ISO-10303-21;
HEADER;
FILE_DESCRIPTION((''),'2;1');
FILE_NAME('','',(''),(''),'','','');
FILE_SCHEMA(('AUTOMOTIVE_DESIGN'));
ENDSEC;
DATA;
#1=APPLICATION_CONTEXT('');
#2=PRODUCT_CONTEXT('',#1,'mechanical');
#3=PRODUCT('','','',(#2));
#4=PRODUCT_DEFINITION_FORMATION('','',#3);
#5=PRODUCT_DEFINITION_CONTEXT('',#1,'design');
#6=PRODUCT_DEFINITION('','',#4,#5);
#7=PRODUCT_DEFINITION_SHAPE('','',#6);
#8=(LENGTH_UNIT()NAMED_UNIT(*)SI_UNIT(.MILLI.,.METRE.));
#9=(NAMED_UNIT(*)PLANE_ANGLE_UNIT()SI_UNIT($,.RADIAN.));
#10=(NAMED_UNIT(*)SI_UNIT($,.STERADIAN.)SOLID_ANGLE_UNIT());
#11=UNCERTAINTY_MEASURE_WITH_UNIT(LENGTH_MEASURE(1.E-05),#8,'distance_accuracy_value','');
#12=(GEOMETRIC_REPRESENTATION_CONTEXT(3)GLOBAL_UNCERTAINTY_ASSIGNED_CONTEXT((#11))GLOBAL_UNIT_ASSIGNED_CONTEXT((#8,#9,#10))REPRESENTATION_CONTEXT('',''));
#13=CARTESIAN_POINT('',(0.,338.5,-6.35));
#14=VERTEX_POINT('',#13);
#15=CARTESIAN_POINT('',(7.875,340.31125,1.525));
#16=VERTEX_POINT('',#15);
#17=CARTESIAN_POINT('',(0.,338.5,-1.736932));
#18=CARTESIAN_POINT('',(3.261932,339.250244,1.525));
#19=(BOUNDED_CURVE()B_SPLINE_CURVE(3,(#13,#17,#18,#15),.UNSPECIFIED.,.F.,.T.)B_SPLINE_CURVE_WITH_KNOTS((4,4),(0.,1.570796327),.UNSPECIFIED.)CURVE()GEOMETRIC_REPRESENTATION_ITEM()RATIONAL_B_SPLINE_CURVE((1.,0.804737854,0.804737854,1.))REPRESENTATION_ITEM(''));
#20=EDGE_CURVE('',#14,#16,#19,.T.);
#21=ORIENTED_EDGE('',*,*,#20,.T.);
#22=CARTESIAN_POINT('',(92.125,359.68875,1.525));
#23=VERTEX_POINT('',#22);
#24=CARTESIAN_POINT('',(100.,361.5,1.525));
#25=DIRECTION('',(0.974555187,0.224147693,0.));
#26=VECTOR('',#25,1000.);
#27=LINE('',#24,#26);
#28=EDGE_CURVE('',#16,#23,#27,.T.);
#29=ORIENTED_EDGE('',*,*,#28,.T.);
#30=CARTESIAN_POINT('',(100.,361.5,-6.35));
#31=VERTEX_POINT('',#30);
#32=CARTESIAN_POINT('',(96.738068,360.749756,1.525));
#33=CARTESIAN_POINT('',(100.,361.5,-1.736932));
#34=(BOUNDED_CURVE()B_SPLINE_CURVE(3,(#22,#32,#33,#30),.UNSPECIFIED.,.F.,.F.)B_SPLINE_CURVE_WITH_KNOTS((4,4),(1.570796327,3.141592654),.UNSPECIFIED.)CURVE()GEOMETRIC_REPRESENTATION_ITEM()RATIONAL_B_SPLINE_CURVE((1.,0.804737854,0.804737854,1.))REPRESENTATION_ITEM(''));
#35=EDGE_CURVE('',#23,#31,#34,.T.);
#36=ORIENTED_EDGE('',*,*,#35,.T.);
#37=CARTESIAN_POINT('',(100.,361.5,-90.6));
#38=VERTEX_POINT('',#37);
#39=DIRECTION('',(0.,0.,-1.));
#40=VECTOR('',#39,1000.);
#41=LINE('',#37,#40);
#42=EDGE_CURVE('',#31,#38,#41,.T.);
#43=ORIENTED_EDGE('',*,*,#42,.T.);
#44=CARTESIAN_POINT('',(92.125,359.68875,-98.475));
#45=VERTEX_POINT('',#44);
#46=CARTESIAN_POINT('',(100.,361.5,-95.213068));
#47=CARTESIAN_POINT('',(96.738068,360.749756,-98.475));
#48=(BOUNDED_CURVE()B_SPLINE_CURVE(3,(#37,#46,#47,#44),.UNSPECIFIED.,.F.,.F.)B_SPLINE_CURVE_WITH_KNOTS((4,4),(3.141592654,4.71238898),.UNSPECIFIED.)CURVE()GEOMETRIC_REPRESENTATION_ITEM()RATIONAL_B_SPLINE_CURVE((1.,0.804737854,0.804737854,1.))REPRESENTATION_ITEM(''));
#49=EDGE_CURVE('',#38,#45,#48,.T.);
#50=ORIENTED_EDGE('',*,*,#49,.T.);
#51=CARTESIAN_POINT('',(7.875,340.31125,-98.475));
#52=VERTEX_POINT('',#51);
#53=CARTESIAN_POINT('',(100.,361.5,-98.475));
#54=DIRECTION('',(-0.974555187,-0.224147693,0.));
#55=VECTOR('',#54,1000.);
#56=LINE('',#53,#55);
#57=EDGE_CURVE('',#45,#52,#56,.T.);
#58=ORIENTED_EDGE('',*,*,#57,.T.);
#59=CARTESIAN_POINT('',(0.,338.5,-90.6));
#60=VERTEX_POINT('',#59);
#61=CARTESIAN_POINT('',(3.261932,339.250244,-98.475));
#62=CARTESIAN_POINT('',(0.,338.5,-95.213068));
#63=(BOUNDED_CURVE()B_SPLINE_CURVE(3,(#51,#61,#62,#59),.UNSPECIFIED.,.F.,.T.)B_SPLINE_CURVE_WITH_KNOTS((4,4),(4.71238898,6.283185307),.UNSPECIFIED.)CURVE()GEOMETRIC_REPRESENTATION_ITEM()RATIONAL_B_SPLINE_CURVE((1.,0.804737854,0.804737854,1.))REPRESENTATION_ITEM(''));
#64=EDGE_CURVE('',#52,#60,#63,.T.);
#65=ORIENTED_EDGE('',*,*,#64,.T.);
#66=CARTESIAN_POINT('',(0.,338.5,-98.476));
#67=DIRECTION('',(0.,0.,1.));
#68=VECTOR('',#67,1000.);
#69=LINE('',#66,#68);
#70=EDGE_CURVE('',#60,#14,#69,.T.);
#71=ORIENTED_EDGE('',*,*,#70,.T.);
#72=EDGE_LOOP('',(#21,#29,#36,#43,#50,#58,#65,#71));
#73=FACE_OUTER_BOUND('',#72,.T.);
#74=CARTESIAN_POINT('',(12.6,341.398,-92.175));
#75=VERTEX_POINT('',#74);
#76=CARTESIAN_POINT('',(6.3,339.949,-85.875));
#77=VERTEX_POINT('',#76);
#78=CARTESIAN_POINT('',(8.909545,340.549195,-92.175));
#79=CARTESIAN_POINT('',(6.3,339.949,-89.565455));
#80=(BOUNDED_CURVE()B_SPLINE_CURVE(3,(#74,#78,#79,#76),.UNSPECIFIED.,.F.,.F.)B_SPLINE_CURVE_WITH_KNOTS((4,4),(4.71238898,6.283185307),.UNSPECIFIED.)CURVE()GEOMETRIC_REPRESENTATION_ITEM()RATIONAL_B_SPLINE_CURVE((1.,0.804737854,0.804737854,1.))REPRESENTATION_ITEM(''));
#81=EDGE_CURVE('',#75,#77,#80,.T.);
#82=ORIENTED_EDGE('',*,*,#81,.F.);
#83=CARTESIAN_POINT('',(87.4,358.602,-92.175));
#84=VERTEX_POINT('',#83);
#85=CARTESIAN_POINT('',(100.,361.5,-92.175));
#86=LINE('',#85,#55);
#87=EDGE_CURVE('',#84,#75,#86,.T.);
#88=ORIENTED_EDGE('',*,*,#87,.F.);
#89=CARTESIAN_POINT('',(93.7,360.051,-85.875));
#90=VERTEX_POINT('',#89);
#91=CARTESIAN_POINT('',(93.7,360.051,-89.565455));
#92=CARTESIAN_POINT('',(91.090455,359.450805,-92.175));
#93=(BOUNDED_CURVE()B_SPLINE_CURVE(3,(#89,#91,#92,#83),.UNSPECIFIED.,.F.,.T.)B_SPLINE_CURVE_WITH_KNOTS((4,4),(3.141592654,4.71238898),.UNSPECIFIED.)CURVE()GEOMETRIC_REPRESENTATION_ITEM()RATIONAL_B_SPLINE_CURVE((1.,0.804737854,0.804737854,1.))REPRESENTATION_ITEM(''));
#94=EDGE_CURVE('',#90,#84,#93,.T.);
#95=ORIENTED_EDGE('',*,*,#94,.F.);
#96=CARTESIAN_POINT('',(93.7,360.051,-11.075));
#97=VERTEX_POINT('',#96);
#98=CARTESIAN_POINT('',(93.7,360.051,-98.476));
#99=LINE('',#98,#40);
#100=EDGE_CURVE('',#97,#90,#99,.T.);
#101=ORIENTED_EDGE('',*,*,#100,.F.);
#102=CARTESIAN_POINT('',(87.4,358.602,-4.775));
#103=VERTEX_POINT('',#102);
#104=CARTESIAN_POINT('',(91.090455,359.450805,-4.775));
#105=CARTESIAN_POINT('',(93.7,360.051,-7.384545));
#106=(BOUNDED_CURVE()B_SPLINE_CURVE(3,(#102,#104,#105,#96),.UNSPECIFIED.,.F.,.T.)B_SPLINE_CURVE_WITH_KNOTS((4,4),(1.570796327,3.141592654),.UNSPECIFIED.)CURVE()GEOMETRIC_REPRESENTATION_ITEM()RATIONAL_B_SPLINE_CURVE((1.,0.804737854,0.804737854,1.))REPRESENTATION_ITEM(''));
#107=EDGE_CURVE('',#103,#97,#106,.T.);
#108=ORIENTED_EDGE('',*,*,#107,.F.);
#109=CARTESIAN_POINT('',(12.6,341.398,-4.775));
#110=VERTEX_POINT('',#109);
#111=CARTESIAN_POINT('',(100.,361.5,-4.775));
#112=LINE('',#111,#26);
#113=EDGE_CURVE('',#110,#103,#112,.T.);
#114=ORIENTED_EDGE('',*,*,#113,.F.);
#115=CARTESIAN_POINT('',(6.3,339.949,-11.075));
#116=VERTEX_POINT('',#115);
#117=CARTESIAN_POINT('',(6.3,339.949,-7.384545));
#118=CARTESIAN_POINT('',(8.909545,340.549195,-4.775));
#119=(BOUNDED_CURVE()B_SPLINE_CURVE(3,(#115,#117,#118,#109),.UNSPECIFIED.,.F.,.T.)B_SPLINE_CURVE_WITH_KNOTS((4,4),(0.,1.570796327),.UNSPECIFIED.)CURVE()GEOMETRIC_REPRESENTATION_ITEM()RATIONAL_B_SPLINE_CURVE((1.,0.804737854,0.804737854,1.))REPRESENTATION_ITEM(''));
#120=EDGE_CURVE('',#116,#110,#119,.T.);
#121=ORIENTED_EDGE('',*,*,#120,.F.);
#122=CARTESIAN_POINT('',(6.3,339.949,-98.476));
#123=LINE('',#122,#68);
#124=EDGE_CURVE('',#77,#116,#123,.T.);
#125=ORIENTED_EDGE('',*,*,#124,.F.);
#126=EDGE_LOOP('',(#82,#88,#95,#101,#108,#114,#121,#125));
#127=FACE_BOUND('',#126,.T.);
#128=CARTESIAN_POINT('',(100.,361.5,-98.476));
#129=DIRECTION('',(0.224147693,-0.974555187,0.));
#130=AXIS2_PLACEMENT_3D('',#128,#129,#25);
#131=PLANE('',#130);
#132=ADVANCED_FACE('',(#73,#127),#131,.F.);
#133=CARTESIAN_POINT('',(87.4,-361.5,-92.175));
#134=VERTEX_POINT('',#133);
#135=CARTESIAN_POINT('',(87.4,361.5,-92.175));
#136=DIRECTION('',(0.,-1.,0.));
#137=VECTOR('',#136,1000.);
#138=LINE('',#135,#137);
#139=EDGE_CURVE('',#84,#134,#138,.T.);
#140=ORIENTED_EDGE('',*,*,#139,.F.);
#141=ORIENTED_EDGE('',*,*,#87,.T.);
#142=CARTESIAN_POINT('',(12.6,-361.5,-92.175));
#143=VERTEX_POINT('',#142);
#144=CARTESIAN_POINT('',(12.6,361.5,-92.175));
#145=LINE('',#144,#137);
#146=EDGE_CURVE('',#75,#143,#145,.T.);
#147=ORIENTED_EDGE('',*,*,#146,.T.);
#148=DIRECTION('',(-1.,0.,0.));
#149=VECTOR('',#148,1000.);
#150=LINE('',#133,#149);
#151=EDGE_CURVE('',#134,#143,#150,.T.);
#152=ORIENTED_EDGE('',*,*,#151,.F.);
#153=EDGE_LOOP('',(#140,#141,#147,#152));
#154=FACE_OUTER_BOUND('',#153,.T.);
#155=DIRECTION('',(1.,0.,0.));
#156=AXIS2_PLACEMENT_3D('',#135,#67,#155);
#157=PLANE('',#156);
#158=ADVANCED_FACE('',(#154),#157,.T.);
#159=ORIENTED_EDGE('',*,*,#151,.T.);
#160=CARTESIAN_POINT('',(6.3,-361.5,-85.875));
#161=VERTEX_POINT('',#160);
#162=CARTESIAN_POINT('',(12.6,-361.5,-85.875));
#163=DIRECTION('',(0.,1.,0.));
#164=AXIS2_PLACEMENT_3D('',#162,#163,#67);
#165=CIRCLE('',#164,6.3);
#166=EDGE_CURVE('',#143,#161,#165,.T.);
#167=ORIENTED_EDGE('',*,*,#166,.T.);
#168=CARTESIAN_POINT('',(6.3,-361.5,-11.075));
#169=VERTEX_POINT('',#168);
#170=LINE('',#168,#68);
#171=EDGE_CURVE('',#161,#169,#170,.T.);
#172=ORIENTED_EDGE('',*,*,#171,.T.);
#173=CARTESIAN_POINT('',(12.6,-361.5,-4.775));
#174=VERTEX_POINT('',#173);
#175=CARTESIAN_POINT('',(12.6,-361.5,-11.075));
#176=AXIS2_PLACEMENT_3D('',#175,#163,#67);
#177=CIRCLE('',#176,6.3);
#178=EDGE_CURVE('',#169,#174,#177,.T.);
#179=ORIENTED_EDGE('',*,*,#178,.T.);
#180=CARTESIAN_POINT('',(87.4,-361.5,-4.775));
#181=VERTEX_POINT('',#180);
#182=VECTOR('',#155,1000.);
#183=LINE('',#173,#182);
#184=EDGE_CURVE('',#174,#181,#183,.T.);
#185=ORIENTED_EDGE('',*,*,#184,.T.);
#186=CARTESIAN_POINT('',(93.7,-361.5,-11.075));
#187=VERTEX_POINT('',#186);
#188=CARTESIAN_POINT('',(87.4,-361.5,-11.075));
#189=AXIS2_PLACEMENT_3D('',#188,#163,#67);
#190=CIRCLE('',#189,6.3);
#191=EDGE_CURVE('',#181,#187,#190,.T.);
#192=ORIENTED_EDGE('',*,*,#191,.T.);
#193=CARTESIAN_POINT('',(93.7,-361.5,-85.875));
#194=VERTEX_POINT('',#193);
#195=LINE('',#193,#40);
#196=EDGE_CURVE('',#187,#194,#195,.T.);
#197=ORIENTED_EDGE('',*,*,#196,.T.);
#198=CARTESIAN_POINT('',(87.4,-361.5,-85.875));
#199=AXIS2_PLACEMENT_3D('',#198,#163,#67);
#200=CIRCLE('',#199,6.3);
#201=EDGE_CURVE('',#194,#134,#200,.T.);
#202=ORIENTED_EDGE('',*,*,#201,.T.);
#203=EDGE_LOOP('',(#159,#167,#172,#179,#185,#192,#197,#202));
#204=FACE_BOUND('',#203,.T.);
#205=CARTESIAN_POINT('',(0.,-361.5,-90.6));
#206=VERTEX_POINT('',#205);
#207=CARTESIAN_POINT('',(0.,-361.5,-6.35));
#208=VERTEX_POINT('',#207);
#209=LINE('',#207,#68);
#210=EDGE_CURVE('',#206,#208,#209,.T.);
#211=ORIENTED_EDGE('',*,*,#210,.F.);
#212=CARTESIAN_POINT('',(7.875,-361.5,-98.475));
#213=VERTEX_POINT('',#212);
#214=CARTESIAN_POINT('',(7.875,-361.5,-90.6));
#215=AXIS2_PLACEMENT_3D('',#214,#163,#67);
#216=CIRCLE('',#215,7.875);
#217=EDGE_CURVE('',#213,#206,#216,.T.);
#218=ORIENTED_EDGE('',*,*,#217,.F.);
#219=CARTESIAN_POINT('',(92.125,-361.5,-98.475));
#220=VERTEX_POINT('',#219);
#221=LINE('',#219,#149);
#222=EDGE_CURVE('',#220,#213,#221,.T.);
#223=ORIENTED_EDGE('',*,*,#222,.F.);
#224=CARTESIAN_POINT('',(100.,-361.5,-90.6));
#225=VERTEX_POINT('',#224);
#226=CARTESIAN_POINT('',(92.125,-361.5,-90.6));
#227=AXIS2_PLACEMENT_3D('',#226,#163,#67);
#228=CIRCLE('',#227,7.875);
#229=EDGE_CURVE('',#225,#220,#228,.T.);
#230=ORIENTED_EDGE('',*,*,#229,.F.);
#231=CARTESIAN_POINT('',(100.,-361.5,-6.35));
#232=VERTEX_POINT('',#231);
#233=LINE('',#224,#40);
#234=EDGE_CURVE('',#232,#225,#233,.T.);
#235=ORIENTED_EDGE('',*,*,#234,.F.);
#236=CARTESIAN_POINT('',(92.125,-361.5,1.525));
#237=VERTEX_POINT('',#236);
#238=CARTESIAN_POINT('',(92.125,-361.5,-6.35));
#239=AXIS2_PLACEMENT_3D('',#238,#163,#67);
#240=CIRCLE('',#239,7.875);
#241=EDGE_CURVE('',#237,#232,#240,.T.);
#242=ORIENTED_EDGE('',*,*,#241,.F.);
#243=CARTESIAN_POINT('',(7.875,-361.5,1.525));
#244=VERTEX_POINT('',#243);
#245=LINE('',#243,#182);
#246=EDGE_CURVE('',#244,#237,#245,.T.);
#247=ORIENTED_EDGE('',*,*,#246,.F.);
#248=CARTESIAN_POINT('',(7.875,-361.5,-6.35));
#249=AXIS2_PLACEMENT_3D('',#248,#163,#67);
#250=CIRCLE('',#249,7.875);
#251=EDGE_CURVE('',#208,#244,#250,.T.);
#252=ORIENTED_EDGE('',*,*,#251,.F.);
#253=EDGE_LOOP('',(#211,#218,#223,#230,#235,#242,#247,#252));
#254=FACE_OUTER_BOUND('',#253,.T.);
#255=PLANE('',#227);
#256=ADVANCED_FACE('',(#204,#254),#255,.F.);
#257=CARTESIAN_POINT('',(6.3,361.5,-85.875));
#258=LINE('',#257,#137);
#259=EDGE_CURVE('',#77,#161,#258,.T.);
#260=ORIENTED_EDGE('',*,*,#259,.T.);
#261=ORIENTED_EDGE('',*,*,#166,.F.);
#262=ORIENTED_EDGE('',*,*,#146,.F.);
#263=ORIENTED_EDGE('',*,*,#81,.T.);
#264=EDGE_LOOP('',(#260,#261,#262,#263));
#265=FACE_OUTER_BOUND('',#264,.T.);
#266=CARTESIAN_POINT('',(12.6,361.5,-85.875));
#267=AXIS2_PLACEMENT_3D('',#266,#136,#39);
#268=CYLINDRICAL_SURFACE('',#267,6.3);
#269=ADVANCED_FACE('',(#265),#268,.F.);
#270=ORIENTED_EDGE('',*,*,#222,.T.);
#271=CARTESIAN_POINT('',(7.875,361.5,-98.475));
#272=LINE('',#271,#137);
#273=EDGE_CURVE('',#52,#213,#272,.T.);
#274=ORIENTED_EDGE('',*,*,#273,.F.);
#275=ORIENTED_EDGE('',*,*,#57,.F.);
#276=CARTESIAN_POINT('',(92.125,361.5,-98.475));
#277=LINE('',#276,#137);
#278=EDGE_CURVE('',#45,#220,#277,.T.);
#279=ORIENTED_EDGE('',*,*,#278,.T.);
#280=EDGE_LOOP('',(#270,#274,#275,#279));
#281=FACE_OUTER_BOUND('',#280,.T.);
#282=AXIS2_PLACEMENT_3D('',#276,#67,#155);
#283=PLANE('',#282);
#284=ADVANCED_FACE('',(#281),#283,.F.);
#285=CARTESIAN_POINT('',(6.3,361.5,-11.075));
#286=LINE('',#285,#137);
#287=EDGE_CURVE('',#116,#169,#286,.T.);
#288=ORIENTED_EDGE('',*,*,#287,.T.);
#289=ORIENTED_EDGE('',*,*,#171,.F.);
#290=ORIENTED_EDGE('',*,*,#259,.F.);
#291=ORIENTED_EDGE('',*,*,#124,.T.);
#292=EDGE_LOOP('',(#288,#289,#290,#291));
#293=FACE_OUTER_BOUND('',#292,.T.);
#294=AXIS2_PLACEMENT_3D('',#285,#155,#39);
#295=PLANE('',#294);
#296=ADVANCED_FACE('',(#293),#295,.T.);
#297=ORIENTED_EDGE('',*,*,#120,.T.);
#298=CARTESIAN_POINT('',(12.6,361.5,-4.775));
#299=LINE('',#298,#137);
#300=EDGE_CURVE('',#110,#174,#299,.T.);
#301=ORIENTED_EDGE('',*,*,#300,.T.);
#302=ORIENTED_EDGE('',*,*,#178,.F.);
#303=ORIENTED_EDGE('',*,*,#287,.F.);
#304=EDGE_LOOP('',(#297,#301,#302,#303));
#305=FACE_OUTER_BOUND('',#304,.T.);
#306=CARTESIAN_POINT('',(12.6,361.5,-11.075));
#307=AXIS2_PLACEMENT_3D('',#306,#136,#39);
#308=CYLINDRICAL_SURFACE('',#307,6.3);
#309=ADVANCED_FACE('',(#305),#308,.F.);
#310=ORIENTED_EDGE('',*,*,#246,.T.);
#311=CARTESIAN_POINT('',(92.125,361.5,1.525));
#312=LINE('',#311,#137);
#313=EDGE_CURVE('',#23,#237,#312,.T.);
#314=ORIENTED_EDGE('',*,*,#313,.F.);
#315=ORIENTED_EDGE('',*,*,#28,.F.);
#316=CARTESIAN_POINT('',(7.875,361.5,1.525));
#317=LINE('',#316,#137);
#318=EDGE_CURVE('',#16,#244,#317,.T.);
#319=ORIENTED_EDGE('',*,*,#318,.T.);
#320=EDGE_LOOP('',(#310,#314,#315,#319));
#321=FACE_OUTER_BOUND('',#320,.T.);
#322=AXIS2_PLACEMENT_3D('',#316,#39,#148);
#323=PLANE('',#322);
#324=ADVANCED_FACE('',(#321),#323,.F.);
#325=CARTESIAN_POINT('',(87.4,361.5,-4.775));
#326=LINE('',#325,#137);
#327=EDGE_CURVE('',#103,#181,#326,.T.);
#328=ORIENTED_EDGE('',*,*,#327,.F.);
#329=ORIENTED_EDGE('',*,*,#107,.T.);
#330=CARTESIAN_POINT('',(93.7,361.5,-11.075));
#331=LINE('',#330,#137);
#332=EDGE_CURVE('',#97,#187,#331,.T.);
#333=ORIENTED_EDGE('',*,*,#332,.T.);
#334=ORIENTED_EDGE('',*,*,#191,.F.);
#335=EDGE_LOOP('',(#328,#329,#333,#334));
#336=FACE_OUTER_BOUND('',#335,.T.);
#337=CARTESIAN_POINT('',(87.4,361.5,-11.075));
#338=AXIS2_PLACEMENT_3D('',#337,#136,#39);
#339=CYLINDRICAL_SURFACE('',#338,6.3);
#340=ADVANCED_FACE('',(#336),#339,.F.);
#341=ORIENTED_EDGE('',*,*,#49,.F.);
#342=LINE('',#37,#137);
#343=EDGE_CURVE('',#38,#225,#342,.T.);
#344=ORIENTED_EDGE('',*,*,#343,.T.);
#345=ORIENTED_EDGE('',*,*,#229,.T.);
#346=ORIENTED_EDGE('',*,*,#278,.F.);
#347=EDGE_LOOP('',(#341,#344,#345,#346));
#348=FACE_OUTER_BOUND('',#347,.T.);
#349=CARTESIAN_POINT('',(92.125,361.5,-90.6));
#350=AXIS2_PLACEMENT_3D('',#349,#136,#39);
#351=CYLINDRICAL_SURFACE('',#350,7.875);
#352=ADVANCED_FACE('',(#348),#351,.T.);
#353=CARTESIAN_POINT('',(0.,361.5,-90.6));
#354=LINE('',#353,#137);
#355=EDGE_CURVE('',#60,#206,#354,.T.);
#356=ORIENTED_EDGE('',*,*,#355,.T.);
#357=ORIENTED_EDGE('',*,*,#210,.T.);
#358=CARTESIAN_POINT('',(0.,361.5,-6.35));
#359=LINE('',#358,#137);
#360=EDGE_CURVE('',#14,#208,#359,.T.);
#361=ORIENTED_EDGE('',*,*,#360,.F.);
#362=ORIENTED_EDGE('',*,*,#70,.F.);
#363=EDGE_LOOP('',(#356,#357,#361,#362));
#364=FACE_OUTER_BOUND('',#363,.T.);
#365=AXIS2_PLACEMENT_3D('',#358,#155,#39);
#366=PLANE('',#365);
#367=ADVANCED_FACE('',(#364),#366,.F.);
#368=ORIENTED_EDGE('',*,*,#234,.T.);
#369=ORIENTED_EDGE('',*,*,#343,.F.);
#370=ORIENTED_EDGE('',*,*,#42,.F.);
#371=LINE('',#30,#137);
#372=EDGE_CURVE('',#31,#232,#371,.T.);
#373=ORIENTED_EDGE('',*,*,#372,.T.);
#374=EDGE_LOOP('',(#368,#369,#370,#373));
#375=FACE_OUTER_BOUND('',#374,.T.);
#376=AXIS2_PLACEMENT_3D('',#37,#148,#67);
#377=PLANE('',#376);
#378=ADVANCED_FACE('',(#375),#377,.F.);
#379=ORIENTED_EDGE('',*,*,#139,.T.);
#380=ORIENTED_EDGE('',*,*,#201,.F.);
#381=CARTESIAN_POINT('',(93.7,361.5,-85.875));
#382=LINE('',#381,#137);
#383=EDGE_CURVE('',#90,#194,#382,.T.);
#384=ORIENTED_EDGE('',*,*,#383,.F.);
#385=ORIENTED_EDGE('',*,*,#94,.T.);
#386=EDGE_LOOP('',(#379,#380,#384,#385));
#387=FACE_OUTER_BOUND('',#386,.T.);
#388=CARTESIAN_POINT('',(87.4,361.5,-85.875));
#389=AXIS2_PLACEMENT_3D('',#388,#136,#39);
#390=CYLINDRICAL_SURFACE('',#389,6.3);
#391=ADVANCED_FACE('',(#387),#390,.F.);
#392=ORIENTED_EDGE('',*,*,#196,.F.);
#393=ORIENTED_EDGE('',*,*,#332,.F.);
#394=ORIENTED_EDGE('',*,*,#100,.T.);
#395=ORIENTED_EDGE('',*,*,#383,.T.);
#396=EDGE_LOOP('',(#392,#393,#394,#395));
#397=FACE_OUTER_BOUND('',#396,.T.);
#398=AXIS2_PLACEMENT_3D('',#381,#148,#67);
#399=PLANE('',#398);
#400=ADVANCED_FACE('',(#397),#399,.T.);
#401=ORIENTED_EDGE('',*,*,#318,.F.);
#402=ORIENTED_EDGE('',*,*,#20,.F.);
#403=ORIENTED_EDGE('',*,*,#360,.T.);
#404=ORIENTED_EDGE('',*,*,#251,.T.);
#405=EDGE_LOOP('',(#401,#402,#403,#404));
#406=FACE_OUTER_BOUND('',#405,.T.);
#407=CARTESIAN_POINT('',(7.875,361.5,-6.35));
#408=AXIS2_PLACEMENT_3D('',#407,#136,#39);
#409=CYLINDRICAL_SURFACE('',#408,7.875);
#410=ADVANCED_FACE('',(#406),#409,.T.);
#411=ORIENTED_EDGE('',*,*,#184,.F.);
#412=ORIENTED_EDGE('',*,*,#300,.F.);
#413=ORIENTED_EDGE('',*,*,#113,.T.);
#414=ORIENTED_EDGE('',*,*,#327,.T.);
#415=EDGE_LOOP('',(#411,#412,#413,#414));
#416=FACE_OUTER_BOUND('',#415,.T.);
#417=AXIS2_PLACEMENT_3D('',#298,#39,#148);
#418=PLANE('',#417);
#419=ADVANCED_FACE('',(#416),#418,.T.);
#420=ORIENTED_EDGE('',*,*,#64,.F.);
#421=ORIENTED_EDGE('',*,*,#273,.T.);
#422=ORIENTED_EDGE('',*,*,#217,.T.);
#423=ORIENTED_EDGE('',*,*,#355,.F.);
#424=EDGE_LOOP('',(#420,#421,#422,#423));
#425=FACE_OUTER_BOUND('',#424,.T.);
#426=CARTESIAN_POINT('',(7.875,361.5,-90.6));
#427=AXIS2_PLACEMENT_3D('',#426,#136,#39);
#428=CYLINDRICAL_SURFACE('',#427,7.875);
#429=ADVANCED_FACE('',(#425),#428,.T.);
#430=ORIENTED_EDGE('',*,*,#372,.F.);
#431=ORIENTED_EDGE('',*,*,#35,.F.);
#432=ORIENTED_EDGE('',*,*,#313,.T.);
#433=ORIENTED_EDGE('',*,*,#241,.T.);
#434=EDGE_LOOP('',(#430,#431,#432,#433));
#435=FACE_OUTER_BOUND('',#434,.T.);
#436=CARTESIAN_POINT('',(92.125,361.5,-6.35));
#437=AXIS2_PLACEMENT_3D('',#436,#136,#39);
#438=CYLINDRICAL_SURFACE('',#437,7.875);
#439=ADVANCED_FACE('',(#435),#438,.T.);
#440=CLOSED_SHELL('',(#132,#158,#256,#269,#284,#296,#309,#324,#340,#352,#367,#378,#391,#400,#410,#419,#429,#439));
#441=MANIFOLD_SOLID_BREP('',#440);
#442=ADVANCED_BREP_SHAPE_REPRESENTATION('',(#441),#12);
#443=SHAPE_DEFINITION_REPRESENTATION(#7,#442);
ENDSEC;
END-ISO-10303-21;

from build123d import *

# Parameters (mm, degrees)
BOSS_EXTRUDE1_DEPTH = 361.5
CUT_EXTRUDE1_REACH  = 390.178


with BuildPart() as part:
    # Sketch2 → Boss-Extrude1 (new, symmetric)
    with BuildSketch(Plane(origin=(0, 0, 0), x_dir=(1, 0, 0), z_dir=(0, 1, 0))):
        with BuildLine():
            Line((7.875, -1.525), (92.125, -1.525))
            ThreePointArc((92.125, -1.525), (97.693465902, 0.781534098), (100, 6.35))
            Line((100, 6.35), (100, 90.6))
            ThreePointArc((100, 90.6), (97.693465902, 96.168465902), (92.125, 98.475))
            Line((92.125, 98.475), (7.875, 98.475))
            ThreePointArc((7.875, 98.475), (2.306534098, 96.168465902), (0, 90.6))
            Line((0, 90.6), (0, 6.35))
            ThreePointArc((0, 6.35), (2.306534098, 0.781534098), (7.875, -1.525))
        make_face()
        with BuildLine():
            Line((12.6, 4.775), (87.4, 4.775))
            ThreePointArc((87.4, 4.775), (91.854772721, 6.620227279), (93.7, 11.075))
            Line((93.7, 11.075), (93.7, 85.875))
            ThreePointArc((93.7, 85.875), (91.854772721, 90.329772721), (87.4, 92.175))
            Line((87.4, 92.175), (12.6, 92.175))
            ThreePointArc((12.6, 92.175), (8.145227279, 90.329772721), (6.3, 85.875))
            Line((6.3, 85.875), (6.3, 11.075))
            ThreePointArc((6.3, 11.075), (8.145227279, 6.620227279), (12.6, 4.775))
        make_face(mode=Mode.SUBTRACT)
    extrude(amount=BOSS_EXTRUDE1_DEPTH, both=True)

    # Sketch4 → Cut-Extrude1 (cut, up to next)
    with BuildSketch(Plane.XY.offset(1.525), mode=Mode.PRIVATE) as cut_extrude1_sk1:
        Polygon((100, 361.5), (0, 338.5), (0, 361.5), align=None)
    cut_extrude1_tool1 = extrude(cut_extrude1_sk1.sketch, amount=-CUT_EXTRUDE1_REACH, mode=Mode.PRIVATE) & part.part
    add(cut_extrude1_tool1.solids().sort_by_distance((33.333333, 353.833333, 1.525))[0], mode=Mode.SUBTRACT)


solid = part.part
